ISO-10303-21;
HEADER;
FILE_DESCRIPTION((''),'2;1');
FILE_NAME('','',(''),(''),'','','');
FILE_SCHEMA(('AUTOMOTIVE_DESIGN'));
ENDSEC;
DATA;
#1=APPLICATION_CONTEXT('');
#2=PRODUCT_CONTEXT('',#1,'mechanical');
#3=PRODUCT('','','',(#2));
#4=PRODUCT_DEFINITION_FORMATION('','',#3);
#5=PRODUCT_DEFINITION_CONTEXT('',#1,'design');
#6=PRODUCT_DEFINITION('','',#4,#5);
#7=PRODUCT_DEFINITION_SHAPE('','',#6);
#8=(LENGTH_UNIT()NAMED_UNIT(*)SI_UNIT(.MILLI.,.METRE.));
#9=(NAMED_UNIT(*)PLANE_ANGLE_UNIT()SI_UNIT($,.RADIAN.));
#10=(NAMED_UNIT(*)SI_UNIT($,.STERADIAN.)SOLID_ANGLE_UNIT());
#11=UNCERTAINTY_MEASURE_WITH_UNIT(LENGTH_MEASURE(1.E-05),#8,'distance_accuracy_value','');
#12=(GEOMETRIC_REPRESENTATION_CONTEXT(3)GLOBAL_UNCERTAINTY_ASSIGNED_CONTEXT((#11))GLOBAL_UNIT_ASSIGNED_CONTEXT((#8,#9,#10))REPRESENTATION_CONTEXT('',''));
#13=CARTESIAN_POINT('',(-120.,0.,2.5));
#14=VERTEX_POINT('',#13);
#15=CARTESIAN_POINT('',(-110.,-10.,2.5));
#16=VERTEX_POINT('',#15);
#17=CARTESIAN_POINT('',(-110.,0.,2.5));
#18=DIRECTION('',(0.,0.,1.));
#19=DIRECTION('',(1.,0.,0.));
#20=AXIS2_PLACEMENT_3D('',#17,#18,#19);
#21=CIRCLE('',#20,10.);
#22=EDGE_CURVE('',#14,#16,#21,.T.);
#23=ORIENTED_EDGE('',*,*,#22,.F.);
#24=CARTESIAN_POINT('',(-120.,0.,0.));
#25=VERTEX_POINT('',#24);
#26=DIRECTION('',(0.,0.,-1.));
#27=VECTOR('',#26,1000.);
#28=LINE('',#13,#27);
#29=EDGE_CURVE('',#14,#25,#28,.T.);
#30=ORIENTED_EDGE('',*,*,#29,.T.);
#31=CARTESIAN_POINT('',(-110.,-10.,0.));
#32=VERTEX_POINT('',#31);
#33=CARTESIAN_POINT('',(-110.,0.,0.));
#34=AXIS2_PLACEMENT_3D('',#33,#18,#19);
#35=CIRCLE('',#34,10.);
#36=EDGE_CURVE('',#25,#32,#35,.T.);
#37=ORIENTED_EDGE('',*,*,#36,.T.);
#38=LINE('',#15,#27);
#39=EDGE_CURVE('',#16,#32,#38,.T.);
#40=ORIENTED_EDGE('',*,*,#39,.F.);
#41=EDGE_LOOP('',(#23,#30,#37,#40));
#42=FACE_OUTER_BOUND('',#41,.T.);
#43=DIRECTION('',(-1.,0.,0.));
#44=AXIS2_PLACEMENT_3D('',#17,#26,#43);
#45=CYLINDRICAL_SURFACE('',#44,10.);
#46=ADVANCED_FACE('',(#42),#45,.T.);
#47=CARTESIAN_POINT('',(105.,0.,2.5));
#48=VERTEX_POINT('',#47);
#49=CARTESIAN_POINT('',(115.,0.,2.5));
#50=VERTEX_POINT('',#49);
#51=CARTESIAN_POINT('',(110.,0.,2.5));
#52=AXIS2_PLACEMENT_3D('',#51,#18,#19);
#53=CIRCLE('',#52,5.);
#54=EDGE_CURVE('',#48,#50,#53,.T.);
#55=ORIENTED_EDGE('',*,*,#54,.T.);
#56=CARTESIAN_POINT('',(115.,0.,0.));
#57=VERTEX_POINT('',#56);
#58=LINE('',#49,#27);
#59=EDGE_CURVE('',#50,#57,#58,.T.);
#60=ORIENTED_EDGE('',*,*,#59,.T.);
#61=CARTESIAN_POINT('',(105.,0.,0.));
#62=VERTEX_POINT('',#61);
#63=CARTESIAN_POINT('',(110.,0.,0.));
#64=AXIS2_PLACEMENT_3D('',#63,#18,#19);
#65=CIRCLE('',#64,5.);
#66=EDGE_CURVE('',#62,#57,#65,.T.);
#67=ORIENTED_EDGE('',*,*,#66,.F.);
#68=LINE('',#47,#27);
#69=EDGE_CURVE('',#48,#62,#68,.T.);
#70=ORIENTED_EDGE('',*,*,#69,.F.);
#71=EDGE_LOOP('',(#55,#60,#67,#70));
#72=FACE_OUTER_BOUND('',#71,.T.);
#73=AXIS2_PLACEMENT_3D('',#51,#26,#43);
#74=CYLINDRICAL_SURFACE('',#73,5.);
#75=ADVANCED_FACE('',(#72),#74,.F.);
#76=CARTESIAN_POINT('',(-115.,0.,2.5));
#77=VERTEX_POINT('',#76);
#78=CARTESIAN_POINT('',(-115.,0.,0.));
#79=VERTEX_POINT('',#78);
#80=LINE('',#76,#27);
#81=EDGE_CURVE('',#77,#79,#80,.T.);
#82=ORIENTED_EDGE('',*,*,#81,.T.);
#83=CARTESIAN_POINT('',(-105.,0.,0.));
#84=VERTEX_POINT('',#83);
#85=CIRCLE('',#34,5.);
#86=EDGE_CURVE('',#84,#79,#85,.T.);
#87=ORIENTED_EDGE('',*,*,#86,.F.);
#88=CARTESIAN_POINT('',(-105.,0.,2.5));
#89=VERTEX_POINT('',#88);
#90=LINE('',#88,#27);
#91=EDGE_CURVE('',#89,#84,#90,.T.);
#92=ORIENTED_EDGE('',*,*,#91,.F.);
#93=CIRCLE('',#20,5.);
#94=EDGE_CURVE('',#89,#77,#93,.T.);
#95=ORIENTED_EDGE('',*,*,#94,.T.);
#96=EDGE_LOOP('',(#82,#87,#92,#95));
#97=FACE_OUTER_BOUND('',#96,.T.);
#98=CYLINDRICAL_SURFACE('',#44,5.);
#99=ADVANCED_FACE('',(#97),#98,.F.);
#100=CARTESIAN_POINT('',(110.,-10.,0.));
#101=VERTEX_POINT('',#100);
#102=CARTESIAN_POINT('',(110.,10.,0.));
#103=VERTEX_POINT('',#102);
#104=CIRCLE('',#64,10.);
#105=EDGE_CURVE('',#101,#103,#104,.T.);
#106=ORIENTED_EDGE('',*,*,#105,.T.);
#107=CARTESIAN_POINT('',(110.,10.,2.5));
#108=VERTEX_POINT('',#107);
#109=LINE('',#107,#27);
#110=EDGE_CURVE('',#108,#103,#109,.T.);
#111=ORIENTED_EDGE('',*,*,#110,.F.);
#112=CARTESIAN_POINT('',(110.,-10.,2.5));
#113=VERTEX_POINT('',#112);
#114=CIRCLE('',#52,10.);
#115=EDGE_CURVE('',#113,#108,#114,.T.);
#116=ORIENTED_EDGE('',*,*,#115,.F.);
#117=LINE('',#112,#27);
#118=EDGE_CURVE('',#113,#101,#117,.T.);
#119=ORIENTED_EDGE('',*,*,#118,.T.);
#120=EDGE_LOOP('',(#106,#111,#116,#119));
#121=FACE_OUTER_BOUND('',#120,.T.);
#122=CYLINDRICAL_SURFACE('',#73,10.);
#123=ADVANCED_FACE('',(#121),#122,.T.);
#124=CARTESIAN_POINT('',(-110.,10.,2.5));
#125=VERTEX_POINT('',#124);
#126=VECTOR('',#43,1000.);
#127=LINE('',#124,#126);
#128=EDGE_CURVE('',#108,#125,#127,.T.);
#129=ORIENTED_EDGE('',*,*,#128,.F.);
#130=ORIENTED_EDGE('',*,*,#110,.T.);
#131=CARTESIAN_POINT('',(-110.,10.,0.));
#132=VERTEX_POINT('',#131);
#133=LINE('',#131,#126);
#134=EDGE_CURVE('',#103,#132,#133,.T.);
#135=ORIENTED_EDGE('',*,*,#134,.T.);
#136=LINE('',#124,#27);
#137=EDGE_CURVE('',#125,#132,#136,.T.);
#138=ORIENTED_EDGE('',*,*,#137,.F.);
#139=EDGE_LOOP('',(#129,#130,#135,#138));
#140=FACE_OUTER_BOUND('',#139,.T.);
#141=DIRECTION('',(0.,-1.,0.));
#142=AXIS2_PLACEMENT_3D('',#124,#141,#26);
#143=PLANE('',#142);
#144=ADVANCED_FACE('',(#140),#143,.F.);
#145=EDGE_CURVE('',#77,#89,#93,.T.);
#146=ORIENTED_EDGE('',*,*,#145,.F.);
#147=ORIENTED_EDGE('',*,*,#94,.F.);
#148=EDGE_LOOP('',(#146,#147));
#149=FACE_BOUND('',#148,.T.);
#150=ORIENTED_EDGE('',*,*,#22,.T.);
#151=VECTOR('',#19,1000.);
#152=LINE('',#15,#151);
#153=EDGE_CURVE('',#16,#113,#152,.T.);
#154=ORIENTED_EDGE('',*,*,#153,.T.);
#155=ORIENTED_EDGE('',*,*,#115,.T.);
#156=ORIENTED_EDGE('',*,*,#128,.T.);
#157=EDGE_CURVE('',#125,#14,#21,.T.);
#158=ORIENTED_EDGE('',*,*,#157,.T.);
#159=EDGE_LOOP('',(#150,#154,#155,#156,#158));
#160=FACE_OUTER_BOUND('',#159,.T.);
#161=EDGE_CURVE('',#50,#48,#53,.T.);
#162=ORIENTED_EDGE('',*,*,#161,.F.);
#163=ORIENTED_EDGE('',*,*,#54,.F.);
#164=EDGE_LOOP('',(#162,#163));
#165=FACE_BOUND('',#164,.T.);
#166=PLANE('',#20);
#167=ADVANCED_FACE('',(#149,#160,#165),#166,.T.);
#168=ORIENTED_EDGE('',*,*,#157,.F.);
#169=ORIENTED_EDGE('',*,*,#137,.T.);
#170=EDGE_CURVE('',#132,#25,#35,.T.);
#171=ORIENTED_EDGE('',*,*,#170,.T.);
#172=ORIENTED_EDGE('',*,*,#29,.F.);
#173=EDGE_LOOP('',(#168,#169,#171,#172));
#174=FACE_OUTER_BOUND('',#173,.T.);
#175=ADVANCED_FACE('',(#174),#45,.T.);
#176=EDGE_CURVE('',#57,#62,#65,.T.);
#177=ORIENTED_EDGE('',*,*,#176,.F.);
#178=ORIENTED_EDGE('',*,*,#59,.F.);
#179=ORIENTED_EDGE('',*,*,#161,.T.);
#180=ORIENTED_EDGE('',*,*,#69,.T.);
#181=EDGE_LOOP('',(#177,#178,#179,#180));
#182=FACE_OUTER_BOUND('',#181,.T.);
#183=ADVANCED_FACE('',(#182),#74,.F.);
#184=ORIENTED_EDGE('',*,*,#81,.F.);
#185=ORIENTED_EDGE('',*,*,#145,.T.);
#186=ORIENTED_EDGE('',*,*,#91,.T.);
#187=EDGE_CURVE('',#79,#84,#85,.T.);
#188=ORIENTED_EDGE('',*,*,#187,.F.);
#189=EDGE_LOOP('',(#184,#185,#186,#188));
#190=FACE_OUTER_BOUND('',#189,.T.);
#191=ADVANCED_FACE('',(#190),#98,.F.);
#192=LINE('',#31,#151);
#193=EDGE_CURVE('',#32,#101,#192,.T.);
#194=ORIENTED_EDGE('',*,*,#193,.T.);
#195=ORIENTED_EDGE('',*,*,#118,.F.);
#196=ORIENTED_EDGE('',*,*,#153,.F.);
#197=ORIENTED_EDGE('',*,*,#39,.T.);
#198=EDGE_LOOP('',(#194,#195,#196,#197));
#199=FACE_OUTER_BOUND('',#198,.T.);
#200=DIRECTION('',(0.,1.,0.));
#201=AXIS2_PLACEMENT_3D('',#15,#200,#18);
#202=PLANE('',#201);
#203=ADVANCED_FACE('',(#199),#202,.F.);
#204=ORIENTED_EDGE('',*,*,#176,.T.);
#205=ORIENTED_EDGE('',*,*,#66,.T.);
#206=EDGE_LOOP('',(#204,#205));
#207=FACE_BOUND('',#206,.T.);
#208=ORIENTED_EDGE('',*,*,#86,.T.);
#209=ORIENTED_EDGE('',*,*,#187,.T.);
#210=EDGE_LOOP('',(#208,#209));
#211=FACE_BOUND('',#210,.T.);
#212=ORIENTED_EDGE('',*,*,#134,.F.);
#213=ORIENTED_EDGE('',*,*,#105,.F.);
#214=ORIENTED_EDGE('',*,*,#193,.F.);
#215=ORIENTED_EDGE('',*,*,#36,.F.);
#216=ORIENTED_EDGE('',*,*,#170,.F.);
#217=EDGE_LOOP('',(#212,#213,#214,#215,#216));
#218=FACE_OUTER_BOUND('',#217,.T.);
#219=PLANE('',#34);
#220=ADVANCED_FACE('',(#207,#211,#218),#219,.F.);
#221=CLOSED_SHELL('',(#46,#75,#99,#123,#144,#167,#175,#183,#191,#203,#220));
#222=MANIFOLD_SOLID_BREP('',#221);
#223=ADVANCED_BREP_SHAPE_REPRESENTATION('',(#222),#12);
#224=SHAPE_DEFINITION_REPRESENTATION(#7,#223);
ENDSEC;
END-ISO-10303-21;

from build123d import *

# Parameters (mm, degrees)
SKETCH1_R           = 5
BOSS_EXTRUDE1_DEPTH = 2.5


with BuildPart() as part:
    # Sketch1 → Boss-Extrude1 (new body)
    with BuildSketch(Plane.XY):
        with BuildLine():
            Line((-110, 10), (110, 10))
            ThreePointArc((110, 10), (120, 0), (110, -10))
            Line((110, -10), (-110, -10))
            ThreePointArc((-110, -10), (-120, 0), (-110, 10))
        make_face()
        with Locations((-110, 0)):
            Circle(SKETCH1_R, mode=Mode.SUBTRACT)
        with Locations((110, 0)):
            Circle(SKETCH1_R, mode=Mode.SUBTRACT)
    extrude(amount=BOSS_EXTRUDE1_DEPTH)


solid = part.part
